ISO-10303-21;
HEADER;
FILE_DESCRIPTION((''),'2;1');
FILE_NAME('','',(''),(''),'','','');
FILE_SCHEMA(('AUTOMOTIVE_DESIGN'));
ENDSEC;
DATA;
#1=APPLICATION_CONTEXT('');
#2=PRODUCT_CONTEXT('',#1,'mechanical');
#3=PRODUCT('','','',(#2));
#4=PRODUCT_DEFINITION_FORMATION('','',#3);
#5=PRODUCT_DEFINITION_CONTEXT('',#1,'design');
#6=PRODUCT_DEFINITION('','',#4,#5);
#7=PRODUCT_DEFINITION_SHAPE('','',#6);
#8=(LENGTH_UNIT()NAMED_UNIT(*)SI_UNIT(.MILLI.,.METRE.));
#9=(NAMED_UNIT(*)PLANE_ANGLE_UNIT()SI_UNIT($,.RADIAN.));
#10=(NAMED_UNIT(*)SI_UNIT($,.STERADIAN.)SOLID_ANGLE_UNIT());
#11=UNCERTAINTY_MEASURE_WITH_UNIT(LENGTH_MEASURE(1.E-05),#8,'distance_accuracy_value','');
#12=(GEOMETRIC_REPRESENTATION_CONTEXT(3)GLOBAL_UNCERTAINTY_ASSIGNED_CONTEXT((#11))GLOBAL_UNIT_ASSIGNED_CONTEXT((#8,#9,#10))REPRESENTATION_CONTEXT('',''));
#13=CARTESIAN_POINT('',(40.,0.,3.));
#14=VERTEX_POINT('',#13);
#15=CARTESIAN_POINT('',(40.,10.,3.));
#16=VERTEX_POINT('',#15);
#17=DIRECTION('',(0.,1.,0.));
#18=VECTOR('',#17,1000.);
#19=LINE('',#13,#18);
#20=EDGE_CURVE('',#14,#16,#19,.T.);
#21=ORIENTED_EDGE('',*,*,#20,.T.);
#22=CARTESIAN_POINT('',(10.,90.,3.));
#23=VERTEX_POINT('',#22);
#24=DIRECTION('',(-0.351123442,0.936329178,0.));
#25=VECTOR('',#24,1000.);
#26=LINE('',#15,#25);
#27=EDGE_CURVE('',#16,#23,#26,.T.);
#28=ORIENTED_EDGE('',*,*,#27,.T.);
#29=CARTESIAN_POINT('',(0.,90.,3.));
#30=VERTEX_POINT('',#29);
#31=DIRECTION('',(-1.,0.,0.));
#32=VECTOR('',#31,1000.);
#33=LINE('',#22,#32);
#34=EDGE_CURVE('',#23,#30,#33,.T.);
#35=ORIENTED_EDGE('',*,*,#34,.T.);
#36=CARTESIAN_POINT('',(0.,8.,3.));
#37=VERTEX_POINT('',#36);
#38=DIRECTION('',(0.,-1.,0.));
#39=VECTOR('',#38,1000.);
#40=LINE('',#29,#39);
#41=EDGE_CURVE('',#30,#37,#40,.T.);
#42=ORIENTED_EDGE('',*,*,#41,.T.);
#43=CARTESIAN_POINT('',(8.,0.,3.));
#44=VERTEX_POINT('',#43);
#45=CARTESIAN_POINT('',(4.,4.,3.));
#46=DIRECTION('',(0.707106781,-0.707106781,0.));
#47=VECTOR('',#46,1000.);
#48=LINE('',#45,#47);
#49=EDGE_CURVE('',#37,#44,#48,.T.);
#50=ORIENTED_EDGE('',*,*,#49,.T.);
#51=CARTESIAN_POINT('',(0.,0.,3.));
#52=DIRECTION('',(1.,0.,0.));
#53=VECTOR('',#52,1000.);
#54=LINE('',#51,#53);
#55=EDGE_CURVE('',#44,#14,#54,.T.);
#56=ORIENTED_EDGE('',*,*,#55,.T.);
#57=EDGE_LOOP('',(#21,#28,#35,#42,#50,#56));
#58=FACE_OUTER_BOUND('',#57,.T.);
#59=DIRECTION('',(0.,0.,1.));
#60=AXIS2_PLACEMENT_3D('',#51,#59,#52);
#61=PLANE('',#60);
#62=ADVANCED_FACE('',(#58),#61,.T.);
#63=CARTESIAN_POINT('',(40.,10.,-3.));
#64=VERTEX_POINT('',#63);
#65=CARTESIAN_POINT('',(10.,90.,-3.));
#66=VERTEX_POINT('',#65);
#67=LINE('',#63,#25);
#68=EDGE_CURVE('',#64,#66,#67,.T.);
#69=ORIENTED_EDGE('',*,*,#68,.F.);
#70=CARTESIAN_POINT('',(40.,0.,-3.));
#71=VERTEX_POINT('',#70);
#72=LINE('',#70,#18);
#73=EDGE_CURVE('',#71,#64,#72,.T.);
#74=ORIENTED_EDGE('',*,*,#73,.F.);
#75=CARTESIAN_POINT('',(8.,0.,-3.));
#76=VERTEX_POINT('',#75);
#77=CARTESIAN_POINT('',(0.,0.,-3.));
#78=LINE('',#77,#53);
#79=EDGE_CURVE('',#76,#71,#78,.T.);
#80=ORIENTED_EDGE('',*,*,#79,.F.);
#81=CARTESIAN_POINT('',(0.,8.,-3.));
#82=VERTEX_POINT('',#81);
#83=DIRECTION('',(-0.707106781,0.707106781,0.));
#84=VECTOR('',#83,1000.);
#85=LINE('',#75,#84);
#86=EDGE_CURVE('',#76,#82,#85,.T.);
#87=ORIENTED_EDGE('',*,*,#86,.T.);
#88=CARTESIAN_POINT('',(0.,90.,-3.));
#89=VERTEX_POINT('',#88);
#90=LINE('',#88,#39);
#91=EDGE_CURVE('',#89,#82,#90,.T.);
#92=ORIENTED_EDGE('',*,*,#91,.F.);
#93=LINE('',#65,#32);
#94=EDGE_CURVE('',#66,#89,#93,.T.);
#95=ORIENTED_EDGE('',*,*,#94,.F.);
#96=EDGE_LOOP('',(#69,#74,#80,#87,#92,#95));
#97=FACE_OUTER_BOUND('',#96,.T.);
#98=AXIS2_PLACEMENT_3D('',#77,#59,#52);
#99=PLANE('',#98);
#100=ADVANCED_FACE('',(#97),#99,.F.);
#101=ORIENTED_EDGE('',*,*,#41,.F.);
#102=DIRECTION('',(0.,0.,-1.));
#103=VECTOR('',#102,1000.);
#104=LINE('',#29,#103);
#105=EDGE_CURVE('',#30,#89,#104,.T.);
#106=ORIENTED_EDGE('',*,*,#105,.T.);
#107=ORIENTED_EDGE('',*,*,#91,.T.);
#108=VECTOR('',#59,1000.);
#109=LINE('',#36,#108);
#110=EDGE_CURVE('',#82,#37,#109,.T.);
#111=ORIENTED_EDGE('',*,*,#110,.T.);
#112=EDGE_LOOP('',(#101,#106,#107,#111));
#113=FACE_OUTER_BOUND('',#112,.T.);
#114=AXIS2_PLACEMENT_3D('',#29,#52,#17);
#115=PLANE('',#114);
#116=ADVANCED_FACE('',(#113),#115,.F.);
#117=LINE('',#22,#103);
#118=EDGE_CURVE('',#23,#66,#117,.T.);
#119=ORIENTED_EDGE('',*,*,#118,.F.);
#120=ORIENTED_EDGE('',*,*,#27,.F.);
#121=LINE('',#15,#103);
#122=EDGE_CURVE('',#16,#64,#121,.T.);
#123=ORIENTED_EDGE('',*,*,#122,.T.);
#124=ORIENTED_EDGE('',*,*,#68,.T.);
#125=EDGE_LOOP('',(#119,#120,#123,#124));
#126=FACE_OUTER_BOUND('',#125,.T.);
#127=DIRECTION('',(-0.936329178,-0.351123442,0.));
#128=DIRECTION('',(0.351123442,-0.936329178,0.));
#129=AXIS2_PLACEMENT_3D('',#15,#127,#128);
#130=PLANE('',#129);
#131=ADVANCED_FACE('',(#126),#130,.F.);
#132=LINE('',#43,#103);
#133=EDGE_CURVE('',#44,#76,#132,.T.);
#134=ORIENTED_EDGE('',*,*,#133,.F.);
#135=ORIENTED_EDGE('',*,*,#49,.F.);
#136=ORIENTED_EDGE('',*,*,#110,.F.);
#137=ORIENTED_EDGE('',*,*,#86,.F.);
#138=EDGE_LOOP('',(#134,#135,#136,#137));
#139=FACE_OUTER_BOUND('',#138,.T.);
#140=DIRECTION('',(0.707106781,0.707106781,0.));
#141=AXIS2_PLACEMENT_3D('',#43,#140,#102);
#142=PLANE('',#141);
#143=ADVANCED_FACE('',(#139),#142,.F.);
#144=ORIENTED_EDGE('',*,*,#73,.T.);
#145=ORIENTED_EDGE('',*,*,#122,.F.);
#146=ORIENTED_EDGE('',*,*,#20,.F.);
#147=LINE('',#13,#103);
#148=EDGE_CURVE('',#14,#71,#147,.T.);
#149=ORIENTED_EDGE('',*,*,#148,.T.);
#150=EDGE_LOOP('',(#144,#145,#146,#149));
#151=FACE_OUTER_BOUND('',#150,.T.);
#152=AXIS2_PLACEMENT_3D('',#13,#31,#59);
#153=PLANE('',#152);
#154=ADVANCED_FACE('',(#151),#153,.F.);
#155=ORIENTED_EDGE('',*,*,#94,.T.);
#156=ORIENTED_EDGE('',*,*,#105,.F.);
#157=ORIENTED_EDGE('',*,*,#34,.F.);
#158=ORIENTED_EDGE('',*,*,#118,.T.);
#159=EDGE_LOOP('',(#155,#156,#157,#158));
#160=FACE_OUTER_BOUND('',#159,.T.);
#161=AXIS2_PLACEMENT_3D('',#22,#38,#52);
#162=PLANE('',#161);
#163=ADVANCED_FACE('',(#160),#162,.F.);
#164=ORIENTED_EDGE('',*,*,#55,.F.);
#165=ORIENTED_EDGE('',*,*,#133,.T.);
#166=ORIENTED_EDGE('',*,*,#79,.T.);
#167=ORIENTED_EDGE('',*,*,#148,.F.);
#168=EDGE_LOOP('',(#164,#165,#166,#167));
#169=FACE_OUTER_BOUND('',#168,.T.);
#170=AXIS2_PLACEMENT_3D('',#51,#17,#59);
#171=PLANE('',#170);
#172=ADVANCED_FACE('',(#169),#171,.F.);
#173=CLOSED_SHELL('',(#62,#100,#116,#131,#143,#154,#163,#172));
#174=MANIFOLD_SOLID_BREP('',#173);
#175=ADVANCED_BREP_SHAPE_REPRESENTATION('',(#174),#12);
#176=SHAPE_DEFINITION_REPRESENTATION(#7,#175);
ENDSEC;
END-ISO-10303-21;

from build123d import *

# Parameters (mm, degrees)
BOSS_EXTRUDE1_DEPTH = 3
CHAMFER1_SIZE       = 8


with BuildPart() as part:
    # Sketch1 → Boss-Extrude1 (new, symmetric)
    with BuildSketch(Plane.XY):
        Polygon((0, 90), (0, 0), (40, 0), (40, 10), (10, 90), align=None)
    extrude(amount=BOSS_EXTRUDE1_DEPTH, both=True)

    # Chamfer1
    chamfer1_edges = [part.edges().sort_by_distance(p)[0] for p in [
        (0, 0, 0),
    ]]
    chamfer(chamfer1_edges, length=CHAMFER1_SIZE)


solid = part.part
